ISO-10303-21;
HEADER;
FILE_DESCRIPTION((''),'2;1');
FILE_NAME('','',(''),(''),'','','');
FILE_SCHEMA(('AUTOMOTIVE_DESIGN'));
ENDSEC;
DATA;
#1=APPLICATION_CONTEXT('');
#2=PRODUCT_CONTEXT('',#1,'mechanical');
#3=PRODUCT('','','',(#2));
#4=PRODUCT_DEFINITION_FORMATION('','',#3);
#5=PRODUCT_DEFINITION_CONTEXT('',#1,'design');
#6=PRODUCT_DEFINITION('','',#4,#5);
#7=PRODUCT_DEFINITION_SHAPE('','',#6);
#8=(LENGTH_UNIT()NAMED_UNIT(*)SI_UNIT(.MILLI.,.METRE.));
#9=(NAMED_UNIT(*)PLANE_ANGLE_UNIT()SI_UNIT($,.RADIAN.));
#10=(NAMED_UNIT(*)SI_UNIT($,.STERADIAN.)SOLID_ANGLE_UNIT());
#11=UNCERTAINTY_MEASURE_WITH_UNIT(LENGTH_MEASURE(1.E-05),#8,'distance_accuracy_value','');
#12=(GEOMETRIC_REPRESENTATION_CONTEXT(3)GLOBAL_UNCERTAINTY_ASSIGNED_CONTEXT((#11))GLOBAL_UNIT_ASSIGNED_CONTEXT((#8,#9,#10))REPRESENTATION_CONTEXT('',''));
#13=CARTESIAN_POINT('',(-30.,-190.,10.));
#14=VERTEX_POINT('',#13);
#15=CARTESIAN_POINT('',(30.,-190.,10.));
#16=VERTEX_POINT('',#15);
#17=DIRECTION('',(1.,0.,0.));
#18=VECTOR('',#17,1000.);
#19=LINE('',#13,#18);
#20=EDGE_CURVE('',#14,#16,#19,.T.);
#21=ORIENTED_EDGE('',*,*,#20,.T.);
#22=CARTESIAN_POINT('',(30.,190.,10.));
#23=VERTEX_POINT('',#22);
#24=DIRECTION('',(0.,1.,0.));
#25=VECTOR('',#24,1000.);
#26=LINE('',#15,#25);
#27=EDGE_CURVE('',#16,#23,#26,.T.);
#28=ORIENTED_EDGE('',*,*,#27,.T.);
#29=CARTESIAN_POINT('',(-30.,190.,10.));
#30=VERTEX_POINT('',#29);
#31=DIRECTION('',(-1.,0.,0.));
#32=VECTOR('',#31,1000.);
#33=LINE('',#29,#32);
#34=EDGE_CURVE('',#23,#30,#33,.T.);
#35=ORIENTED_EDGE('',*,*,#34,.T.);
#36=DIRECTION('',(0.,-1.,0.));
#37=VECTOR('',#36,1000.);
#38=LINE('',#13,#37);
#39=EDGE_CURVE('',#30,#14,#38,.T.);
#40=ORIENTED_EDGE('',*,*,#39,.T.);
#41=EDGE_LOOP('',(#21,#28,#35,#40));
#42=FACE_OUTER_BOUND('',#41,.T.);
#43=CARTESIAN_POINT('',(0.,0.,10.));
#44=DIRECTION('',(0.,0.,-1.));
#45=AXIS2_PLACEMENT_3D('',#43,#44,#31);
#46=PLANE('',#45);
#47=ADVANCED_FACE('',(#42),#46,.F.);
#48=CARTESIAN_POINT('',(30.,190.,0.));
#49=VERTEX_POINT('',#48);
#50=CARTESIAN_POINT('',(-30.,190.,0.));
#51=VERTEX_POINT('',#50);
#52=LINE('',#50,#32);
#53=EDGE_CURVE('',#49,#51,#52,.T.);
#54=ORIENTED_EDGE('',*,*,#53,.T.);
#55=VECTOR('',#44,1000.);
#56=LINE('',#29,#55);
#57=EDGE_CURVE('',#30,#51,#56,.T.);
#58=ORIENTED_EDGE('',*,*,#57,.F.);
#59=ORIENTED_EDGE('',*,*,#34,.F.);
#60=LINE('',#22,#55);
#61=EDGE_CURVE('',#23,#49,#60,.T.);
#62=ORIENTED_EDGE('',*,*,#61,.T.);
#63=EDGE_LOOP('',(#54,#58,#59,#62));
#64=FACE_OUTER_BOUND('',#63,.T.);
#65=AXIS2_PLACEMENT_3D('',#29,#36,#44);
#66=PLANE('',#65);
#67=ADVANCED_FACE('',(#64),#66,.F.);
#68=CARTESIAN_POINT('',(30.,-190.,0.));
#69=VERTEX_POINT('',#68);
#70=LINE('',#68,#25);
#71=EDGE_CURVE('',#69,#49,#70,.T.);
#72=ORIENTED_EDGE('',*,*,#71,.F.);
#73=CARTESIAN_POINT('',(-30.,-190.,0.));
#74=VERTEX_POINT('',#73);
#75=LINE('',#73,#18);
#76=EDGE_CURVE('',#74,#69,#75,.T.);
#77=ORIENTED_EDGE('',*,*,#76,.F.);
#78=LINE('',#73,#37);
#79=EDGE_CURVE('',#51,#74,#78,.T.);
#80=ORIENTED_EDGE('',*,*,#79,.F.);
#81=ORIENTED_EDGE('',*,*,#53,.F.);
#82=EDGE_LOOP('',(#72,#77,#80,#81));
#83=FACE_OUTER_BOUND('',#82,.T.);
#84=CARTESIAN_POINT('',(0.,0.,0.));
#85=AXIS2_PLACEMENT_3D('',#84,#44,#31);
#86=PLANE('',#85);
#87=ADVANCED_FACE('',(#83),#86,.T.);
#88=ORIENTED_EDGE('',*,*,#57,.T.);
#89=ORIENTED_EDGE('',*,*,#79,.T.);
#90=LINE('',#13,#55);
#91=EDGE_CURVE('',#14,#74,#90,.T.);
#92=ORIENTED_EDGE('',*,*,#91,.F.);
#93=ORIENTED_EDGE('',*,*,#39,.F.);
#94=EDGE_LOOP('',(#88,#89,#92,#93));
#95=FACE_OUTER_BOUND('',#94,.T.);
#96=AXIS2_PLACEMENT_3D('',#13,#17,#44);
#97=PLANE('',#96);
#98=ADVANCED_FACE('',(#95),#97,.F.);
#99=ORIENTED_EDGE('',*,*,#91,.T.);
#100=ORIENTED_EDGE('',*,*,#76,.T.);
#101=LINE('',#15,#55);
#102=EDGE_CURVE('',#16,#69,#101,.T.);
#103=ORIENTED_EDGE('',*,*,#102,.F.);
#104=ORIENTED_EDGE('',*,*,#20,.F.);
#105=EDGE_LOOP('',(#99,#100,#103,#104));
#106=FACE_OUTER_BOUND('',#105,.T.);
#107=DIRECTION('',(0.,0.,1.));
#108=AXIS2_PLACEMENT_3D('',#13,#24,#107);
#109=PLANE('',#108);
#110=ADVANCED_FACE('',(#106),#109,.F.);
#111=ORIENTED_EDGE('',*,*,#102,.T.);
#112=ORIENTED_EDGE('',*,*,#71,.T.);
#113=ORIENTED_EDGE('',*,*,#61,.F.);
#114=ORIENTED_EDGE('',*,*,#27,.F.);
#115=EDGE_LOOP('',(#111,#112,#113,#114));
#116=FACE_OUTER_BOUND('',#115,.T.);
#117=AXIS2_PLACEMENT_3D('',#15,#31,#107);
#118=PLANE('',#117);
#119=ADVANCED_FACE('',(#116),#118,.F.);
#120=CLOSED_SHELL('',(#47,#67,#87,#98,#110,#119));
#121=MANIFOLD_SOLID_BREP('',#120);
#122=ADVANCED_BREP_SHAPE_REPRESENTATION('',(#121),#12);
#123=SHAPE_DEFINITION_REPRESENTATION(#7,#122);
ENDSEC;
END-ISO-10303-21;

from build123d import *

# Parameters (mm, degrees)
SKETCH_1_W      = 60
SKETCH_1_H      = 380
EXTRUDE_1_DEPTH = 10


with BuildPart() as part:
    # 草图1 → 凸台-拉伸1 (new body)
    with BuildSketch(Plane.XY):
        Rectangle(SKETCH_1_W, SKETCH_1_H)
    extrude(amount=EXTRUDE_1_DEPTH)


solid = part.part
